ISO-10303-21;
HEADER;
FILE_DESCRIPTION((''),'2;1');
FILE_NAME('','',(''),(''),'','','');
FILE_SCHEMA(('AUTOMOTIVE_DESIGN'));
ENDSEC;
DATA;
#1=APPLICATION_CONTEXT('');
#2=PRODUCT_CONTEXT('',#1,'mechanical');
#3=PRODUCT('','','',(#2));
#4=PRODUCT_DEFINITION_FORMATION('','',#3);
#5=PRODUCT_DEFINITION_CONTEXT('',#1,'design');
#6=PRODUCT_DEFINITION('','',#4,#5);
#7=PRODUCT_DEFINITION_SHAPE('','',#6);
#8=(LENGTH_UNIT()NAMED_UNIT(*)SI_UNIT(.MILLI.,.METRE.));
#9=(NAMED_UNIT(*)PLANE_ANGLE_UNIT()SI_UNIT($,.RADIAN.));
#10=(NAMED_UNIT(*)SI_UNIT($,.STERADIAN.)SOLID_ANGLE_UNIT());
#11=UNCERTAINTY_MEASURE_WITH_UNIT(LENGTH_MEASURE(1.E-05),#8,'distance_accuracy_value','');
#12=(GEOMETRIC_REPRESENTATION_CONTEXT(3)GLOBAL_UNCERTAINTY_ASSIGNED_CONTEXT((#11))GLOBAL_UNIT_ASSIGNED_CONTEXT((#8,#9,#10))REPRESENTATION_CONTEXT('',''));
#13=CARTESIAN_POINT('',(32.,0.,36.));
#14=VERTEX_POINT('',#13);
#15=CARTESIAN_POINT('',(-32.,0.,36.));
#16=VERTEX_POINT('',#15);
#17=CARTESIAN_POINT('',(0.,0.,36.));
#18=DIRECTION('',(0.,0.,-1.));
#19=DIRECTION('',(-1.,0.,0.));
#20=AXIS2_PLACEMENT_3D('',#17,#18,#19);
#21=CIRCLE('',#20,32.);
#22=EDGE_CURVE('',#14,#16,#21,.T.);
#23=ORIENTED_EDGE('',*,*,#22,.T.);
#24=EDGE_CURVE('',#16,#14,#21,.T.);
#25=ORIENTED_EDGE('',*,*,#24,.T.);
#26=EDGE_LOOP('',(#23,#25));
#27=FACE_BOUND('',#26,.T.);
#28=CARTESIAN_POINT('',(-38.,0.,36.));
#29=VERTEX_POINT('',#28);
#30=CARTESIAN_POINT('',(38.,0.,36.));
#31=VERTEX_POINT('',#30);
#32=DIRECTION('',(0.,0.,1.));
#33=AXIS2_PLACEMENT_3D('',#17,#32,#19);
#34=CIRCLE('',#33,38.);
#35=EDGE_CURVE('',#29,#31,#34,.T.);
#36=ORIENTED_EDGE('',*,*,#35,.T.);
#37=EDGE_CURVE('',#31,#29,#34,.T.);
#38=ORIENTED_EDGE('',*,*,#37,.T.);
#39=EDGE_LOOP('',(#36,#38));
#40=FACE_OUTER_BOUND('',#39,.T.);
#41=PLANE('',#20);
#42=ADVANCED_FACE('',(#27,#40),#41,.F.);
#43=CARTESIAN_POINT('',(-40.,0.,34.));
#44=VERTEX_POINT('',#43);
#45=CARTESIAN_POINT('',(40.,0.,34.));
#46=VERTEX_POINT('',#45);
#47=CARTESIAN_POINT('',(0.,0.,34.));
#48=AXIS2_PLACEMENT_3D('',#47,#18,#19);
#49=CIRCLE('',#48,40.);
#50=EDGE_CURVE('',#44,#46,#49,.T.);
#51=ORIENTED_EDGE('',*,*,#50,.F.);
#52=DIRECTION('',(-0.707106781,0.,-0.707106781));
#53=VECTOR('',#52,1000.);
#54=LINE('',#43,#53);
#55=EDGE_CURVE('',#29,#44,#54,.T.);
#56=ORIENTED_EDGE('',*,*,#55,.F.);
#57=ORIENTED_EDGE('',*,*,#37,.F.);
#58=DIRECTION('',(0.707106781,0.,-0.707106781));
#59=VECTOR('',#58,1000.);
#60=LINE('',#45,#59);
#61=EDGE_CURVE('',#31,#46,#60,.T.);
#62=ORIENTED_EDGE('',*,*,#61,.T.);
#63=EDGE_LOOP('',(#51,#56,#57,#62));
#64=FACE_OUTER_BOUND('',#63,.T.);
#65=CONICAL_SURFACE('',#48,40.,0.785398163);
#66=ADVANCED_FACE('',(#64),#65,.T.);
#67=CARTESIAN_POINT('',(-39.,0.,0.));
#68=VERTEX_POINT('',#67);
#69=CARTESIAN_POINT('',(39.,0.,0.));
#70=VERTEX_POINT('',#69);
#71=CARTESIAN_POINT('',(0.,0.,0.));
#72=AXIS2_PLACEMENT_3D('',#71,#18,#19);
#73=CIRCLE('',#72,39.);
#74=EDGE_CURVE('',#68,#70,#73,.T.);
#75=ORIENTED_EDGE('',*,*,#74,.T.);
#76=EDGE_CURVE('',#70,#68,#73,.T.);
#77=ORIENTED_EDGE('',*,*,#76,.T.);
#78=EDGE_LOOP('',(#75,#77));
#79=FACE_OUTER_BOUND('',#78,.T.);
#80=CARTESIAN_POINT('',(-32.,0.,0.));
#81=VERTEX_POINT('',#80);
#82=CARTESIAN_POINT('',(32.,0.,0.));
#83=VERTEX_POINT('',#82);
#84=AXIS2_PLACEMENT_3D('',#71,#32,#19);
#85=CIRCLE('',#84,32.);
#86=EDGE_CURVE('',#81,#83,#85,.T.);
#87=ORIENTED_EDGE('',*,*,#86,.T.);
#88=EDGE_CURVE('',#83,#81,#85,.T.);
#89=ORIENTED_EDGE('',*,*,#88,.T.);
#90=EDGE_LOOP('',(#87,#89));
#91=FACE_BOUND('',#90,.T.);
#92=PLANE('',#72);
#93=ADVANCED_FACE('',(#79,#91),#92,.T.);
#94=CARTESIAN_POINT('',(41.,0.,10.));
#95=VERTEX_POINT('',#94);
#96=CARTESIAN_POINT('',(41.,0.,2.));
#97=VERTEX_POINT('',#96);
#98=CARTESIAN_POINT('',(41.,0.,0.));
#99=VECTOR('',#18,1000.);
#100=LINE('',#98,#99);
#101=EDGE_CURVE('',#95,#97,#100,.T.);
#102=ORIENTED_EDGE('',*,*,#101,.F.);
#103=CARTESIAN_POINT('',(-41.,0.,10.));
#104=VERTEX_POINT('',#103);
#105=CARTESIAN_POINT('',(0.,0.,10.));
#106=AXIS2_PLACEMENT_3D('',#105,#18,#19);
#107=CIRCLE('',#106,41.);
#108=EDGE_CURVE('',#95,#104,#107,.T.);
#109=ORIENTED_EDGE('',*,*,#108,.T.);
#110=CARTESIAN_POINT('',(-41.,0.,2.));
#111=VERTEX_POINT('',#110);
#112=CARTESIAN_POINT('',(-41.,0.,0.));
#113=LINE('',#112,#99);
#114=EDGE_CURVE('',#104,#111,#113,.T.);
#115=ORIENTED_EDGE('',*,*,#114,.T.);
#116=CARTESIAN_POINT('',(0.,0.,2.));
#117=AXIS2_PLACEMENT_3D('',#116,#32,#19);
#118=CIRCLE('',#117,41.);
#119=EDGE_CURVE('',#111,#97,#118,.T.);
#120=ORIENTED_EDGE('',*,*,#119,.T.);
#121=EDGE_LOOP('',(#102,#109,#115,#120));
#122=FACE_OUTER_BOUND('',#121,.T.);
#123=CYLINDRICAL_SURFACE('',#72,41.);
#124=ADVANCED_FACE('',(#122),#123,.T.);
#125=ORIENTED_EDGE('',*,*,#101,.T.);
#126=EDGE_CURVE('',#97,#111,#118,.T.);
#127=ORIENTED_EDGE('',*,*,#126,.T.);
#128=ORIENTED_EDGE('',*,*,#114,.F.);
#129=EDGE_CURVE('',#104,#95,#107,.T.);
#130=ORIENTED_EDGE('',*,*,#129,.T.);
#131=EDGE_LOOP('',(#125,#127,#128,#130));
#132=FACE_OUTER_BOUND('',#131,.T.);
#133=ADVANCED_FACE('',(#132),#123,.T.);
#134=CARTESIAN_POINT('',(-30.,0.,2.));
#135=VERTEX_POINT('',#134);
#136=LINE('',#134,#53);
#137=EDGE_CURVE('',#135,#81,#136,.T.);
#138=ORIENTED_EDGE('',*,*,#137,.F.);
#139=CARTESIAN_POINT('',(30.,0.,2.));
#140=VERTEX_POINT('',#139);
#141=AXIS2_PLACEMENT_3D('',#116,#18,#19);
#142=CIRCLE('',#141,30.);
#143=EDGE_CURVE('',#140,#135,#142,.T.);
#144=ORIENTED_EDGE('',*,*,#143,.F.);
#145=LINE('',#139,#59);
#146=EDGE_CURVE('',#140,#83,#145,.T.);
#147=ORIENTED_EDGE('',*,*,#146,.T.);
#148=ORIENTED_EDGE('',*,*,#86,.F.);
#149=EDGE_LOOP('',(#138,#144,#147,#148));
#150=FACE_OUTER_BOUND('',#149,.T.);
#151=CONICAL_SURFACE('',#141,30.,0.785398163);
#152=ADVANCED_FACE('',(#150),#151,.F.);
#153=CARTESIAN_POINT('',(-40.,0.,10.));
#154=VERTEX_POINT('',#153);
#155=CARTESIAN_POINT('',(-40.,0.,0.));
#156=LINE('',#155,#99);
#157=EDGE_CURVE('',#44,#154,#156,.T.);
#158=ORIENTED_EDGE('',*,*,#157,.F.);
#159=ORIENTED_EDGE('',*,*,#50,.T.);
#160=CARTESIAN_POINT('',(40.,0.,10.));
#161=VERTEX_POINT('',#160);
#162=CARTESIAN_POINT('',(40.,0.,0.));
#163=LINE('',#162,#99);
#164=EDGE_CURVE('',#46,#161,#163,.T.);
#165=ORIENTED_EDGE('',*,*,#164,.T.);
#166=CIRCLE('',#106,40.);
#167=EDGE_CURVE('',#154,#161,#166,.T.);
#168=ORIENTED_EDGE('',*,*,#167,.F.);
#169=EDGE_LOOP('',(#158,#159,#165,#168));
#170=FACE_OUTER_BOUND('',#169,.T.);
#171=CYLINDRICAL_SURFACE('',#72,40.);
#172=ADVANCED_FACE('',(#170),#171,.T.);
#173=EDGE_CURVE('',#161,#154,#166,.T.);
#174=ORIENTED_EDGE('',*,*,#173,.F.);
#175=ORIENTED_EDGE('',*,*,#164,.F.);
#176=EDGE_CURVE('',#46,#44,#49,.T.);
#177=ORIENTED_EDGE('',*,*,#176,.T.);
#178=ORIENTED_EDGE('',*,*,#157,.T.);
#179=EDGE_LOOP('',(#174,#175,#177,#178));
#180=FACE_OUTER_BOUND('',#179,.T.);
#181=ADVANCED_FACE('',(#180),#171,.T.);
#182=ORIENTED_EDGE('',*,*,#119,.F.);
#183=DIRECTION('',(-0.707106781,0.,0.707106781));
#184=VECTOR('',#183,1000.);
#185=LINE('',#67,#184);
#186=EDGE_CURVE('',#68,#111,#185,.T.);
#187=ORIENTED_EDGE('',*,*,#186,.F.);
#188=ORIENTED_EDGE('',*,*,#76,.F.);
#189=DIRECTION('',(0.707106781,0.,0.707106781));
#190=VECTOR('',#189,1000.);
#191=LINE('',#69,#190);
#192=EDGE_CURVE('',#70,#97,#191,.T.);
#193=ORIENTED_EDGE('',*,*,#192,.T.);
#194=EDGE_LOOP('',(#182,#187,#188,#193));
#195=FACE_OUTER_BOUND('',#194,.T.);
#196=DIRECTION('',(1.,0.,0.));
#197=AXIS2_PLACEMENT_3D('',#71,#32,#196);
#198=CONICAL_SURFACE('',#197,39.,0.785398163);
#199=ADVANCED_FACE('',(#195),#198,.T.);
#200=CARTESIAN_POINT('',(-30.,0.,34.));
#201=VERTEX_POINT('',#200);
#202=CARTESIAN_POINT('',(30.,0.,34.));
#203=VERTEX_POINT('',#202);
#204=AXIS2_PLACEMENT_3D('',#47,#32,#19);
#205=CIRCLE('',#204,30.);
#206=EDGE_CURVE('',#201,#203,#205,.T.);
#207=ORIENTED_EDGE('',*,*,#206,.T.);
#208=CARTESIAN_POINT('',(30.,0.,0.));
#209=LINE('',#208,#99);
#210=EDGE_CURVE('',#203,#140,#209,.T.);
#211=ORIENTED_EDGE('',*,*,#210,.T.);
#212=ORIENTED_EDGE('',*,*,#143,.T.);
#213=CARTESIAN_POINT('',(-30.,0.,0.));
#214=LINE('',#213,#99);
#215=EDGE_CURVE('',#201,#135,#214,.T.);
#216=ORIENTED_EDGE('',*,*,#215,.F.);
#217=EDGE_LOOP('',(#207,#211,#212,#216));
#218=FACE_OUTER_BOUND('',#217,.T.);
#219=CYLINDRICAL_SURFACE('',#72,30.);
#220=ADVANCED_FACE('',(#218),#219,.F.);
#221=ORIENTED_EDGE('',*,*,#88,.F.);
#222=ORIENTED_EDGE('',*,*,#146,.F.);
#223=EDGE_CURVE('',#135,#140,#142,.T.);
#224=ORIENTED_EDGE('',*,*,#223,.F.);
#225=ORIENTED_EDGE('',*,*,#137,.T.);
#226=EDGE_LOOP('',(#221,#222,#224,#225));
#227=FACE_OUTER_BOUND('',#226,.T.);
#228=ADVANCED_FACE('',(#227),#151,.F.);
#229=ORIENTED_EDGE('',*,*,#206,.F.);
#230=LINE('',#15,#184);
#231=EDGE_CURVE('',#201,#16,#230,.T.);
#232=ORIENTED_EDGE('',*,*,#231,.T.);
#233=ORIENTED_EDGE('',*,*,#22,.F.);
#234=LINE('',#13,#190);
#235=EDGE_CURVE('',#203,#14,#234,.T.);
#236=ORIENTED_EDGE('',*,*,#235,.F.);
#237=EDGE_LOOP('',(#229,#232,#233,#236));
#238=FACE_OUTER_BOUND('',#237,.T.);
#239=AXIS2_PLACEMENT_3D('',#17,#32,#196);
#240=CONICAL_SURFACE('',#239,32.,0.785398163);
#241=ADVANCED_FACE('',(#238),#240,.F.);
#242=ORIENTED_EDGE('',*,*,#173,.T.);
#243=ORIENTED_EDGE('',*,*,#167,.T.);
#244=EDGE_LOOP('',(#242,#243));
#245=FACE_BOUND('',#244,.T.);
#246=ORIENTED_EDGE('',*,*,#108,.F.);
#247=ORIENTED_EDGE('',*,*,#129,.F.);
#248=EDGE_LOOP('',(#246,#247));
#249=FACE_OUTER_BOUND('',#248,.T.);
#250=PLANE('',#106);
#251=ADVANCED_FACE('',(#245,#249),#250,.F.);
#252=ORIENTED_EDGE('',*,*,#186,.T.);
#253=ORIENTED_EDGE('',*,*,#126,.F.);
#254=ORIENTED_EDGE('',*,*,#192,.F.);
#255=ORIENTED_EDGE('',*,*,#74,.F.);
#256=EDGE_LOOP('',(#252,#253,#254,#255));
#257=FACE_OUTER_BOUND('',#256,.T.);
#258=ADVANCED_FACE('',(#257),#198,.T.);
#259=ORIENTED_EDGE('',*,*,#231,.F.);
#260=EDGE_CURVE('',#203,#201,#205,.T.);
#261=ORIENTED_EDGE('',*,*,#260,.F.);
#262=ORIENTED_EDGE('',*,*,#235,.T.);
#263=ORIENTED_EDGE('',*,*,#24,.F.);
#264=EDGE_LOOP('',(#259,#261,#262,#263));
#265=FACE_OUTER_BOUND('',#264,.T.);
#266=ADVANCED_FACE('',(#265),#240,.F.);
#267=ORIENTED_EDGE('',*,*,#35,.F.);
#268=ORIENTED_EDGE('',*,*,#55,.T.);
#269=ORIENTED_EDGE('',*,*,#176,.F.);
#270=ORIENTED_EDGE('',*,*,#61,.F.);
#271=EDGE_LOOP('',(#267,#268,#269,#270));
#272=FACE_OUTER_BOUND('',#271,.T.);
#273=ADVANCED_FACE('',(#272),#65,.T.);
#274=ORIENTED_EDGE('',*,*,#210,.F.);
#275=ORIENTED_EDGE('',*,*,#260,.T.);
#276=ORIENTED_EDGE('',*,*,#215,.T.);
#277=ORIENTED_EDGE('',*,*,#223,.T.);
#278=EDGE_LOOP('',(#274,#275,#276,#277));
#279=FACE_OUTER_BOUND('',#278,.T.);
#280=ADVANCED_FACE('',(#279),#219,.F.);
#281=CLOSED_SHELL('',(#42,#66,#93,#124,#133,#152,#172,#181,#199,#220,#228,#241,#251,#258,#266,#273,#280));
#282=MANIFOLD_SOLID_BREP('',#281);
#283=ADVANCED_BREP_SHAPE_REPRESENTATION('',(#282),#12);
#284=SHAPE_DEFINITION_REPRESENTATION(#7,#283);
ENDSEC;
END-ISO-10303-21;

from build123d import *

# Parameters (mm, degrees)
SKETCH1_W     = 26
SKETCH1_H     = 10
SKETCH1_W_2   = 10
SKETCH1_H_2   = 1
CHAMFER1_SIZE = 2


with BuildPart() as part:
    # Sketch1 → Revolve1 (revolve)
    with BuildSketch(Plane(origin=(0, 0, 0), x_dir=(0, 0, -1), z_dir=(1, 0, 0)), mode=Mode.PRIVATE) as revolve1_sk:
        with Locations((-23, 35)):
            Rectangle(SKETCH1_W, SKETCH1_H)
        with Locations((-5, 35)):
            Rectangle(SKETCH1_W_2, SKETCH1_H)
        with Locations((-5, 40.5)):
            Rectangle(SKETCH1_W_2, SKETCH1_H_2)
    revolve(revolve1_sk.sketch.rotate(Axis((0, 0, 0), (0, 0, 1)), 90), axis=Axis((0, 0, 0), (0, 0, 1)))

    # Chamfer1
    chamfer1_edges = [part.edges().sort_by_distance(p)[0] for p in [
        (30, 0, 36),
        (40, 0, 36),
        (41, 0, 0),
        (30, 0, 0),
    ]]
    chamfer(chamfer1_edges, length=CHAMFER1_SIZE)


solid = part.part
